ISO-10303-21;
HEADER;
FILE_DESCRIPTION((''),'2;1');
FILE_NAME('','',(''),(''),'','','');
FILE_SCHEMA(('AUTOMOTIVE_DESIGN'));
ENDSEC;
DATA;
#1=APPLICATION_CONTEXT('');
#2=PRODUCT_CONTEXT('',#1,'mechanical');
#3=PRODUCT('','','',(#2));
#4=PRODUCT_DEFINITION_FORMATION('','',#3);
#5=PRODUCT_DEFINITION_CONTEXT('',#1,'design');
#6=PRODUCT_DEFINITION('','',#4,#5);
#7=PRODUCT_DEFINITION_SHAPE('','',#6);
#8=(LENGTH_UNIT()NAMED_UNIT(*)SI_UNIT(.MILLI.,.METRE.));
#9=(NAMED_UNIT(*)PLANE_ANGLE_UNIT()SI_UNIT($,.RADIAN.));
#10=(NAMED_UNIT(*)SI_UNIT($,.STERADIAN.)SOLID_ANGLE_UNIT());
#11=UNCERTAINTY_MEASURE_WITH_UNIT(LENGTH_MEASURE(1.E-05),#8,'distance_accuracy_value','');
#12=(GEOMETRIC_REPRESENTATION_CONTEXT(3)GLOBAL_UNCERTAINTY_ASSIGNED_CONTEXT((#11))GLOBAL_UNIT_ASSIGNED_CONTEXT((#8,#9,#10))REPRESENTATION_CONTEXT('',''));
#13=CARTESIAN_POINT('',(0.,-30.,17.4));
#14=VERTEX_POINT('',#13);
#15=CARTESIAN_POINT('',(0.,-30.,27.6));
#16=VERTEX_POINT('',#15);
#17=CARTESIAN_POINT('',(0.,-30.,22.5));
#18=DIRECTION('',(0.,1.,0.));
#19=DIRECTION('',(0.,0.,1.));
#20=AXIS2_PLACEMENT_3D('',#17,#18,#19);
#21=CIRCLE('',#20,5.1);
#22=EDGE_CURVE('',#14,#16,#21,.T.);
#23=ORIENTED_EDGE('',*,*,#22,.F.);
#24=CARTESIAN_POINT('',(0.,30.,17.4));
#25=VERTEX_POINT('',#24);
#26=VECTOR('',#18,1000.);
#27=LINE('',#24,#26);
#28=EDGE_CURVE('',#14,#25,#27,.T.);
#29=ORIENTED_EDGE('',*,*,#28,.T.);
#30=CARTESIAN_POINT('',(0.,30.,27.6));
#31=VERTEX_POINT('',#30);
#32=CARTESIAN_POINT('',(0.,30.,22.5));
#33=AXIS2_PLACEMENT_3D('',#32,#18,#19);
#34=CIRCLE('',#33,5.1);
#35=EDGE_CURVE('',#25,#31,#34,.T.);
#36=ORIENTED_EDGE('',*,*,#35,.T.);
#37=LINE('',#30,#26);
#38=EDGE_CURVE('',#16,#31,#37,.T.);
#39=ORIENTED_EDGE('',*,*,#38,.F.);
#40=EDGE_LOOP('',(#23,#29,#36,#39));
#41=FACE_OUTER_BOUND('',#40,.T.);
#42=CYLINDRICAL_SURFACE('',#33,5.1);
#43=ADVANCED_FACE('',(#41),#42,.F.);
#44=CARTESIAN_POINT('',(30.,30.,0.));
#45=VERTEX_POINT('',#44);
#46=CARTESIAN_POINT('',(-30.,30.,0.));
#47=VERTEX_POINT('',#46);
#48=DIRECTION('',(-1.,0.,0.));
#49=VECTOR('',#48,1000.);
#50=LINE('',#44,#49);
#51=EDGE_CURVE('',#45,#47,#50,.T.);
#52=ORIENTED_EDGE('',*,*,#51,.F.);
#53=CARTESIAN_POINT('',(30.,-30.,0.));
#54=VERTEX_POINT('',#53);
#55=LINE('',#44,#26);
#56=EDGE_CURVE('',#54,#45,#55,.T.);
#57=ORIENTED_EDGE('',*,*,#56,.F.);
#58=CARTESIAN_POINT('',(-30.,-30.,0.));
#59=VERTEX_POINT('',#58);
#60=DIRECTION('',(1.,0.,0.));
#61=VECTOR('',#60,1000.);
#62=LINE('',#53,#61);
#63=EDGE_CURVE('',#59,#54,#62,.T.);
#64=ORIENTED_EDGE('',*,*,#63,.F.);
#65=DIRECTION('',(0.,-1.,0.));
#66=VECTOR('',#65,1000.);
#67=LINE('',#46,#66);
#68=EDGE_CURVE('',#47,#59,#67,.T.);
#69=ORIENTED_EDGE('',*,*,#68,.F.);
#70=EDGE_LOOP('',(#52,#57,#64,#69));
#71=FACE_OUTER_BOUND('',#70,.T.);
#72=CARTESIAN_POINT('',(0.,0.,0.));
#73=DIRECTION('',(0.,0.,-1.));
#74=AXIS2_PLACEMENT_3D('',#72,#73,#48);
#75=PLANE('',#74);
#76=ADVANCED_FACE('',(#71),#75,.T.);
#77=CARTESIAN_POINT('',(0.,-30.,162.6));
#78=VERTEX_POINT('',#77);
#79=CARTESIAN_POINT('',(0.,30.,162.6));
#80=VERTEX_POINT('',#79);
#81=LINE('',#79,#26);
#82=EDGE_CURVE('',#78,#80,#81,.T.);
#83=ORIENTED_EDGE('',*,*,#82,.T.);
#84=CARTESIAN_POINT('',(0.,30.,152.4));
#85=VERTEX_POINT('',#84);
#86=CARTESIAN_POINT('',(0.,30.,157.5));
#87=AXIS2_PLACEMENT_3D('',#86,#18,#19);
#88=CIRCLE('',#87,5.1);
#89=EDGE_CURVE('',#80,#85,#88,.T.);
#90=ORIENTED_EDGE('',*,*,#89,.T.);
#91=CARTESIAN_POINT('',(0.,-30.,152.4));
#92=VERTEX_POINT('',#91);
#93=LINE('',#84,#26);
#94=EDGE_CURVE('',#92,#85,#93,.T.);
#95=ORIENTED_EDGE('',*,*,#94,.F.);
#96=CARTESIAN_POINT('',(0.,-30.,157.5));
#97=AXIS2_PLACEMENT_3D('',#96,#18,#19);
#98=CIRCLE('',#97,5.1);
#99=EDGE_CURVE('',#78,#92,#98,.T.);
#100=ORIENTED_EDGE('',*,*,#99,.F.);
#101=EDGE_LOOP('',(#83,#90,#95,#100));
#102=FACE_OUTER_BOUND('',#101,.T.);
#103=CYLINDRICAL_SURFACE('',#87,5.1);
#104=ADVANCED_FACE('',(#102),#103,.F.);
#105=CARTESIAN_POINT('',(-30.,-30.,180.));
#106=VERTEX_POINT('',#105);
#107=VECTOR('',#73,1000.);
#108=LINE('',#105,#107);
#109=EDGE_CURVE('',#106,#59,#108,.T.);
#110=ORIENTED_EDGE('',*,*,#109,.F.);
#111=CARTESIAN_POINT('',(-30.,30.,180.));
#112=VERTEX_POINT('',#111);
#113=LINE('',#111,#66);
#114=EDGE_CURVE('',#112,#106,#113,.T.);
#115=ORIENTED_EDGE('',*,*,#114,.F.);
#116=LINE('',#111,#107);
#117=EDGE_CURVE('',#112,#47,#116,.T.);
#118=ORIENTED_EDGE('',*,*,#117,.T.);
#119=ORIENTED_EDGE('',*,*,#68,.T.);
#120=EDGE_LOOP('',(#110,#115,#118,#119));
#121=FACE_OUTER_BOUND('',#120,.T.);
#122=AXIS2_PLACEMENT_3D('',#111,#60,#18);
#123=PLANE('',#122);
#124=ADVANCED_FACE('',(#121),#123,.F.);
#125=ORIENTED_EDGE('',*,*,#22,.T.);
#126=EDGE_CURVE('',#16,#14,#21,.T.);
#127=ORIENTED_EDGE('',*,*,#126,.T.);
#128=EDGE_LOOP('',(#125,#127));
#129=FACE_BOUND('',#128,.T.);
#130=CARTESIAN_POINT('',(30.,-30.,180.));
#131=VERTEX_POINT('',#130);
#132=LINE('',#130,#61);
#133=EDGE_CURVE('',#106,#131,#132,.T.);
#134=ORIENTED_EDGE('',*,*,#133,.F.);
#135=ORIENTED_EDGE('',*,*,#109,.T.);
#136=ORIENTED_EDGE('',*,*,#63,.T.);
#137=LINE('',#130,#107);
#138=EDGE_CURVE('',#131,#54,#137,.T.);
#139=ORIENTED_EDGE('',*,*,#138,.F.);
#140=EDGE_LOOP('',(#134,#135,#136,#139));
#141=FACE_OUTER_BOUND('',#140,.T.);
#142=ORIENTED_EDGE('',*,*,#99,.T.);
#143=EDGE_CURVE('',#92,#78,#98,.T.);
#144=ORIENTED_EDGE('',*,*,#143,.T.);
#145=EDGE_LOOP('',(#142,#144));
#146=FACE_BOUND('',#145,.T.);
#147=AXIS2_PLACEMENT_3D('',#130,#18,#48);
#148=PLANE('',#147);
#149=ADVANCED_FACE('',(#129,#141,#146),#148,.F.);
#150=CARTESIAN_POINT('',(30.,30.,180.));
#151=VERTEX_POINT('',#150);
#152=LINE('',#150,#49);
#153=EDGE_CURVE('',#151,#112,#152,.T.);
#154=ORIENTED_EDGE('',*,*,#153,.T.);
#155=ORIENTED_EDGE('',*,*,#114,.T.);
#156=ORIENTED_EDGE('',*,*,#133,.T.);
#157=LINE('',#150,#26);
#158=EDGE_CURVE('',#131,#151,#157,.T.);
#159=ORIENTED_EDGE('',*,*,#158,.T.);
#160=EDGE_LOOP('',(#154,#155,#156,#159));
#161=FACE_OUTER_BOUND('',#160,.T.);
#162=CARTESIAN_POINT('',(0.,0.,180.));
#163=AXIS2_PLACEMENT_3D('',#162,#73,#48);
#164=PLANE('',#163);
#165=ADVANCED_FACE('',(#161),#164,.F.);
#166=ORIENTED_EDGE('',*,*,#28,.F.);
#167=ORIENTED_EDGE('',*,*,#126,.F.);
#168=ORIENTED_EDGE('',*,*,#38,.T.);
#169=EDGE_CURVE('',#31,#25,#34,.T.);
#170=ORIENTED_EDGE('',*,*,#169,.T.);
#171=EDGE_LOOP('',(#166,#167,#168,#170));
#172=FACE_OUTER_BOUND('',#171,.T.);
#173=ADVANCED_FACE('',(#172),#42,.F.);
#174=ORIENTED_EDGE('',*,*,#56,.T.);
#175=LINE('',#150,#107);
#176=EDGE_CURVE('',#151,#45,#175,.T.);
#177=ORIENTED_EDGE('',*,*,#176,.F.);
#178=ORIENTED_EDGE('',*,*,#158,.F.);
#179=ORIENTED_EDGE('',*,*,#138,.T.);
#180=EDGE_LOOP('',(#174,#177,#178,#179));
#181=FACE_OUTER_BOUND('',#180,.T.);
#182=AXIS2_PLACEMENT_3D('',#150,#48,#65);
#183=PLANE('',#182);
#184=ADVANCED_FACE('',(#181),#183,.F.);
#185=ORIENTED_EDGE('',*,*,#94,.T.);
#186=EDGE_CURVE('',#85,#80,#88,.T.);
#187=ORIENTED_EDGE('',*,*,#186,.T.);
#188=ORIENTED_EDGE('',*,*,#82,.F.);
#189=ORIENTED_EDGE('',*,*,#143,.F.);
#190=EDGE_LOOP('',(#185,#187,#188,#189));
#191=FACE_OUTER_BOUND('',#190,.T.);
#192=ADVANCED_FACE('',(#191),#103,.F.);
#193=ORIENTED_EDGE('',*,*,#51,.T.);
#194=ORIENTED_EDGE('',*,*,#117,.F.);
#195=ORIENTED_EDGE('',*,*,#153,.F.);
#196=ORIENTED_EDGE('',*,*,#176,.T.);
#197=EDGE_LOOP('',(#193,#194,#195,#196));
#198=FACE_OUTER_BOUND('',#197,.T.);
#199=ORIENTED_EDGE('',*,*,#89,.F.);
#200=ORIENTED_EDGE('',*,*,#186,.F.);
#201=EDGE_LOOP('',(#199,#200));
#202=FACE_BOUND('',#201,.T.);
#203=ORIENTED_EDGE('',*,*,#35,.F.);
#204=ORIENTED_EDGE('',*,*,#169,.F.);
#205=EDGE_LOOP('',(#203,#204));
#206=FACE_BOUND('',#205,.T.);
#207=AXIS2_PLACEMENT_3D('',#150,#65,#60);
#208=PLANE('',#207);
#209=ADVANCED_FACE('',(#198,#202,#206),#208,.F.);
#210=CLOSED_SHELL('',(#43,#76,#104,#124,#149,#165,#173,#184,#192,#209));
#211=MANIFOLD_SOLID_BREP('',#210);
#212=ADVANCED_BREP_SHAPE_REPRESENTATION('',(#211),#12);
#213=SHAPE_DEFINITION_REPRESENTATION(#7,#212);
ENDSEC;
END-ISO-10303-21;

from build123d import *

# Parameters (mm, degrees)
SKETCH1_W           = 60
SKETCH1_H           = 60
BOSS_EXTRUDE1_DEPTH = 180
M12_TAPPED_HOLE1_D  = 10.2


with BuildPart() as part:
    # Sketch1 → Boss-Extrude1 (new body)
    with BuildSketch(Plane.XY):
        Rectangle(SKETCH1_W, SKETCH1_H)
    extrude(amount=BOSS_EXTRUDE1_DEPTH)

    # M12 Tapped Hole1 (through all)
    with Locations(Plane(origin=(0, 30, 0), x_dir=(1, 0, 0), z_dir=(0, 1, 0))):
        with Locations((0, -22.5), (0, -157.5)):
            Hole(M12_TAPPED_HOLE1_D / 2)


solid = part.part
